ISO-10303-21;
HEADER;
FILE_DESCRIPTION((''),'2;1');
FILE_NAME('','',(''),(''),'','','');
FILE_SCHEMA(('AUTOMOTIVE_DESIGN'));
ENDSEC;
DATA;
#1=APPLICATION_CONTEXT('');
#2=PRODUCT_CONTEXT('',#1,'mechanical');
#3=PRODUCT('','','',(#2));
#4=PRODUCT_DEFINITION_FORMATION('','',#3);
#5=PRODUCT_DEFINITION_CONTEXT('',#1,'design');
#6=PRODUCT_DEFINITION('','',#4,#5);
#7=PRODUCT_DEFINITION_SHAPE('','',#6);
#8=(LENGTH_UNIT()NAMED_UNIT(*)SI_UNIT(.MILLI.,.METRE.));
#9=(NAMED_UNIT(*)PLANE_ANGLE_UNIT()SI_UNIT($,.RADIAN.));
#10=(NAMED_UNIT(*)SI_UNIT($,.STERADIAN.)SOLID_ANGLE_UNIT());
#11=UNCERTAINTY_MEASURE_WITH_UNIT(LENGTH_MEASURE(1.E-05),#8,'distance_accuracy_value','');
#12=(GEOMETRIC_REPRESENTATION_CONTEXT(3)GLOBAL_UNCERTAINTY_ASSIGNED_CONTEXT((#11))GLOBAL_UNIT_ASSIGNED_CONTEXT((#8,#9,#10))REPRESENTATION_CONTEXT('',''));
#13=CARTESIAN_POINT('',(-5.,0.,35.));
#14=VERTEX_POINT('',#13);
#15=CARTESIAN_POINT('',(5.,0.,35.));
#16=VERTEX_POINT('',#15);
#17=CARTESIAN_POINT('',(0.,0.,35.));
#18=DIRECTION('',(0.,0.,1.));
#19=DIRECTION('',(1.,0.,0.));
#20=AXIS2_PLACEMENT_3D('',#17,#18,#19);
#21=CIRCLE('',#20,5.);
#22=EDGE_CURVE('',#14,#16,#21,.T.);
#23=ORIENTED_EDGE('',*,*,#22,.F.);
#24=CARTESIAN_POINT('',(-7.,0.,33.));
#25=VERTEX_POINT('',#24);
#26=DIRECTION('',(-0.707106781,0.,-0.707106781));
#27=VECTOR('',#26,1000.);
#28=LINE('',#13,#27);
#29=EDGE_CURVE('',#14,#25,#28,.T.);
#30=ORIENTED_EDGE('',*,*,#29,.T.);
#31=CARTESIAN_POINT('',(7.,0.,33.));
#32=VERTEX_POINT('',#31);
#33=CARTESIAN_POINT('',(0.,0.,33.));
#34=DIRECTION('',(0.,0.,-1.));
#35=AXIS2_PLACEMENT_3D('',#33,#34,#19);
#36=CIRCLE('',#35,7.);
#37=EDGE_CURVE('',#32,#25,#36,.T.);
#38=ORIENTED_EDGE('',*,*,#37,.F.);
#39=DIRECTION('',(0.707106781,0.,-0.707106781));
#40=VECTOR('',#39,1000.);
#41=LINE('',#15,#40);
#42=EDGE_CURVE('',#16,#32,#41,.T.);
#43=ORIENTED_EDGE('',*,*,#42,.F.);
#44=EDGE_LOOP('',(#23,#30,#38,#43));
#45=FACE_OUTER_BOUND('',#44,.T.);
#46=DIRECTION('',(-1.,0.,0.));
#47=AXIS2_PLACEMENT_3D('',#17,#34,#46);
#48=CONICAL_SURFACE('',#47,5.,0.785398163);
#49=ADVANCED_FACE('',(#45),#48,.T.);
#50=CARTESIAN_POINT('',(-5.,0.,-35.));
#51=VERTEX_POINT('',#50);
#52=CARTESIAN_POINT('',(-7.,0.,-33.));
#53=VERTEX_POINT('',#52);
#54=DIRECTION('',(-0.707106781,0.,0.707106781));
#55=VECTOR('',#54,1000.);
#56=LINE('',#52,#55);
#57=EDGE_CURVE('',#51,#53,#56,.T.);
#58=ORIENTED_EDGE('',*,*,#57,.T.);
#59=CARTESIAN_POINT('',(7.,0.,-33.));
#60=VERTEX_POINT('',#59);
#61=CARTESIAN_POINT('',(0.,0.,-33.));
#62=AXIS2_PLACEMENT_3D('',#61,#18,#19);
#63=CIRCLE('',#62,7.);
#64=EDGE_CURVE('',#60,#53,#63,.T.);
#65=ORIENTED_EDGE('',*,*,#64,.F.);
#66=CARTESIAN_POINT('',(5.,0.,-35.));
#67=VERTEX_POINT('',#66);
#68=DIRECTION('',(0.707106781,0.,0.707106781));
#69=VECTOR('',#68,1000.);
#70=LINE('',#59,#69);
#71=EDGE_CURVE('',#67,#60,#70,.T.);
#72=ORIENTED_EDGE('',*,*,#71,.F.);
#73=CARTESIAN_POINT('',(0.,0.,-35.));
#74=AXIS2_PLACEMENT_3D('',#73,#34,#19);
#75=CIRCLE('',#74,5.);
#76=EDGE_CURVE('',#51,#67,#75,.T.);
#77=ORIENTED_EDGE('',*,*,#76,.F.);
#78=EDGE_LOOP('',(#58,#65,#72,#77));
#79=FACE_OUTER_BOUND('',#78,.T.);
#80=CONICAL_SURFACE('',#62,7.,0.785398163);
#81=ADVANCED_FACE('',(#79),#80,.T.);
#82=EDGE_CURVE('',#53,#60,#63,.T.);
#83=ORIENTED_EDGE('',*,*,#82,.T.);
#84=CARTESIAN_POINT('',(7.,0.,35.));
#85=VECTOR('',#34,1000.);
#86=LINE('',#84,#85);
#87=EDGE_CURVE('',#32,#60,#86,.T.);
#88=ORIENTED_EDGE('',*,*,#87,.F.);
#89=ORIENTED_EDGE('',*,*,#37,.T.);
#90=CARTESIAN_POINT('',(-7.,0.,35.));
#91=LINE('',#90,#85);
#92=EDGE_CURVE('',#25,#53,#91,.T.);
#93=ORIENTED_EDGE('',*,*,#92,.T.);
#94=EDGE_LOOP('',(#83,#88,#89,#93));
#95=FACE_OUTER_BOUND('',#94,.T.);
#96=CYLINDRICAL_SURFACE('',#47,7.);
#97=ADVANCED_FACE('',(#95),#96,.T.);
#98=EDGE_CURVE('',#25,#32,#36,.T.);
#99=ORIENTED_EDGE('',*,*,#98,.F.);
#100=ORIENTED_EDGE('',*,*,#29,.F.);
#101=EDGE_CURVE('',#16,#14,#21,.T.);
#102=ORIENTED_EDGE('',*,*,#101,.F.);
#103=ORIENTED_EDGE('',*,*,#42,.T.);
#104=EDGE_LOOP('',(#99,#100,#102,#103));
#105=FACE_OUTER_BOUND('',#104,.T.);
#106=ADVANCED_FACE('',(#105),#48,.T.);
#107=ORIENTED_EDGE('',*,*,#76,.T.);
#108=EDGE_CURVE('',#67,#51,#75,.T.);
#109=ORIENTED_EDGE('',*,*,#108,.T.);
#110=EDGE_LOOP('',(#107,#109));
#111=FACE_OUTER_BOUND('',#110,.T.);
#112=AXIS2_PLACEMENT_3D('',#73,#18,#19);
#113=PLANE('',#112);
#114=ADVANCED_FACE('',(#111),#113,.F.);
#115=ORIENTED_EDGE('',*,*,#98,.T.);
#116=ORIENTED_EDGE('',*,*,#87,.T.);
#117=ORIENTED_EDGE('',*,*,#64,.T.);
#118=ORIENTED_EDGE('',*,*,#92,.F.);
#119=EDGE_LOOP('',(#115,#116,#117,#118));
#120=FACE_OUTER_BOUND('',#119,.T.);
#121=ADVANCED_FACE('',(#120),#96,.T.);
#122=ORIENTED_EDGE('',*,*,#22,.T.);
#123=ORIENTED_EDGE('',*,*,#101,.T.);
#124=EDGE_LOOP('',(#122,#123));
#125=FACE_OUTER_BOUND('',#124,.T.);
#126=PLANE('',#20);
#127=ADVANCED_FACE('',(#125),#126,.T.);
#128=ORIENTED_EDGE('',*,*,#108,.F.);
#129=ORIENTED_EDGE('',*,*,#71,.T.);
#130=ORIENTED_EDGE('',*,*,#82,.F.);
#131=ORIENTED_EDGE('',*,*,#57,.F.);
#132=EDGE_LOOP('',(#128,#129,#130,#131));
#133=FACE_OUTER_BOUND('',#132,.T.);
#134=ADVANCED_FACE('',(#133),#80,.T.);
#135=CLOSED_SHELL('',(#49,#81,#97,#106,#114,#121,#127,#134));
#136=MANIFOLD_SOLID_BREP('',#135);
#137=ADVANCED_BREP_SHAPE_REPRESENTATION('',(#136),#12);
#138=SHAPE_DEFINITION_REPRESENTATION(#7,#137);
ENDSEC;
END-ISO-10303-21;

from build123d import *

# Parameters (mm, degrees)
PIN_PROFILE_14_R        = 7
PIN_BODY_14X70_DEPTH    = 35
END_CHAMFER_2X45_A_SIZE = 2
END_CHAMFER_2X45_B_SIZE = 2


with BuildPart() as part:
    # Pin Profile Ø14 → Pin Body Ø14x70 (new, symmetric)
    with BuildSketch(Plane.XY):
        Circle(PIN_PROFILE_14_R)
    extrude(amount=PIN_BODY_14X70_DEPTH, both=True)

    # End Chamfer 2x45 A
    end_chamfer_2x45_a_edges = [part.edges().sort_by_distance(p)[0] for p in [
        (-7, 0, 35),
    ]]
    chamfer(end_chamfer_2x45_a_edges, length=END_CHAMFER_2X45_A_SIZE)

    # End Chamfer 2x45 B
    end_chamfer_2x45_b_edges = [part.edges().sort_by_distance(p)[0] for p in [
        (-7, 0, -35),
    ]]
    chamfer(end_chamfer_2x45_b_edges, length=END_CHAMFER_2X45_B_SIZE)


solid = part.part
